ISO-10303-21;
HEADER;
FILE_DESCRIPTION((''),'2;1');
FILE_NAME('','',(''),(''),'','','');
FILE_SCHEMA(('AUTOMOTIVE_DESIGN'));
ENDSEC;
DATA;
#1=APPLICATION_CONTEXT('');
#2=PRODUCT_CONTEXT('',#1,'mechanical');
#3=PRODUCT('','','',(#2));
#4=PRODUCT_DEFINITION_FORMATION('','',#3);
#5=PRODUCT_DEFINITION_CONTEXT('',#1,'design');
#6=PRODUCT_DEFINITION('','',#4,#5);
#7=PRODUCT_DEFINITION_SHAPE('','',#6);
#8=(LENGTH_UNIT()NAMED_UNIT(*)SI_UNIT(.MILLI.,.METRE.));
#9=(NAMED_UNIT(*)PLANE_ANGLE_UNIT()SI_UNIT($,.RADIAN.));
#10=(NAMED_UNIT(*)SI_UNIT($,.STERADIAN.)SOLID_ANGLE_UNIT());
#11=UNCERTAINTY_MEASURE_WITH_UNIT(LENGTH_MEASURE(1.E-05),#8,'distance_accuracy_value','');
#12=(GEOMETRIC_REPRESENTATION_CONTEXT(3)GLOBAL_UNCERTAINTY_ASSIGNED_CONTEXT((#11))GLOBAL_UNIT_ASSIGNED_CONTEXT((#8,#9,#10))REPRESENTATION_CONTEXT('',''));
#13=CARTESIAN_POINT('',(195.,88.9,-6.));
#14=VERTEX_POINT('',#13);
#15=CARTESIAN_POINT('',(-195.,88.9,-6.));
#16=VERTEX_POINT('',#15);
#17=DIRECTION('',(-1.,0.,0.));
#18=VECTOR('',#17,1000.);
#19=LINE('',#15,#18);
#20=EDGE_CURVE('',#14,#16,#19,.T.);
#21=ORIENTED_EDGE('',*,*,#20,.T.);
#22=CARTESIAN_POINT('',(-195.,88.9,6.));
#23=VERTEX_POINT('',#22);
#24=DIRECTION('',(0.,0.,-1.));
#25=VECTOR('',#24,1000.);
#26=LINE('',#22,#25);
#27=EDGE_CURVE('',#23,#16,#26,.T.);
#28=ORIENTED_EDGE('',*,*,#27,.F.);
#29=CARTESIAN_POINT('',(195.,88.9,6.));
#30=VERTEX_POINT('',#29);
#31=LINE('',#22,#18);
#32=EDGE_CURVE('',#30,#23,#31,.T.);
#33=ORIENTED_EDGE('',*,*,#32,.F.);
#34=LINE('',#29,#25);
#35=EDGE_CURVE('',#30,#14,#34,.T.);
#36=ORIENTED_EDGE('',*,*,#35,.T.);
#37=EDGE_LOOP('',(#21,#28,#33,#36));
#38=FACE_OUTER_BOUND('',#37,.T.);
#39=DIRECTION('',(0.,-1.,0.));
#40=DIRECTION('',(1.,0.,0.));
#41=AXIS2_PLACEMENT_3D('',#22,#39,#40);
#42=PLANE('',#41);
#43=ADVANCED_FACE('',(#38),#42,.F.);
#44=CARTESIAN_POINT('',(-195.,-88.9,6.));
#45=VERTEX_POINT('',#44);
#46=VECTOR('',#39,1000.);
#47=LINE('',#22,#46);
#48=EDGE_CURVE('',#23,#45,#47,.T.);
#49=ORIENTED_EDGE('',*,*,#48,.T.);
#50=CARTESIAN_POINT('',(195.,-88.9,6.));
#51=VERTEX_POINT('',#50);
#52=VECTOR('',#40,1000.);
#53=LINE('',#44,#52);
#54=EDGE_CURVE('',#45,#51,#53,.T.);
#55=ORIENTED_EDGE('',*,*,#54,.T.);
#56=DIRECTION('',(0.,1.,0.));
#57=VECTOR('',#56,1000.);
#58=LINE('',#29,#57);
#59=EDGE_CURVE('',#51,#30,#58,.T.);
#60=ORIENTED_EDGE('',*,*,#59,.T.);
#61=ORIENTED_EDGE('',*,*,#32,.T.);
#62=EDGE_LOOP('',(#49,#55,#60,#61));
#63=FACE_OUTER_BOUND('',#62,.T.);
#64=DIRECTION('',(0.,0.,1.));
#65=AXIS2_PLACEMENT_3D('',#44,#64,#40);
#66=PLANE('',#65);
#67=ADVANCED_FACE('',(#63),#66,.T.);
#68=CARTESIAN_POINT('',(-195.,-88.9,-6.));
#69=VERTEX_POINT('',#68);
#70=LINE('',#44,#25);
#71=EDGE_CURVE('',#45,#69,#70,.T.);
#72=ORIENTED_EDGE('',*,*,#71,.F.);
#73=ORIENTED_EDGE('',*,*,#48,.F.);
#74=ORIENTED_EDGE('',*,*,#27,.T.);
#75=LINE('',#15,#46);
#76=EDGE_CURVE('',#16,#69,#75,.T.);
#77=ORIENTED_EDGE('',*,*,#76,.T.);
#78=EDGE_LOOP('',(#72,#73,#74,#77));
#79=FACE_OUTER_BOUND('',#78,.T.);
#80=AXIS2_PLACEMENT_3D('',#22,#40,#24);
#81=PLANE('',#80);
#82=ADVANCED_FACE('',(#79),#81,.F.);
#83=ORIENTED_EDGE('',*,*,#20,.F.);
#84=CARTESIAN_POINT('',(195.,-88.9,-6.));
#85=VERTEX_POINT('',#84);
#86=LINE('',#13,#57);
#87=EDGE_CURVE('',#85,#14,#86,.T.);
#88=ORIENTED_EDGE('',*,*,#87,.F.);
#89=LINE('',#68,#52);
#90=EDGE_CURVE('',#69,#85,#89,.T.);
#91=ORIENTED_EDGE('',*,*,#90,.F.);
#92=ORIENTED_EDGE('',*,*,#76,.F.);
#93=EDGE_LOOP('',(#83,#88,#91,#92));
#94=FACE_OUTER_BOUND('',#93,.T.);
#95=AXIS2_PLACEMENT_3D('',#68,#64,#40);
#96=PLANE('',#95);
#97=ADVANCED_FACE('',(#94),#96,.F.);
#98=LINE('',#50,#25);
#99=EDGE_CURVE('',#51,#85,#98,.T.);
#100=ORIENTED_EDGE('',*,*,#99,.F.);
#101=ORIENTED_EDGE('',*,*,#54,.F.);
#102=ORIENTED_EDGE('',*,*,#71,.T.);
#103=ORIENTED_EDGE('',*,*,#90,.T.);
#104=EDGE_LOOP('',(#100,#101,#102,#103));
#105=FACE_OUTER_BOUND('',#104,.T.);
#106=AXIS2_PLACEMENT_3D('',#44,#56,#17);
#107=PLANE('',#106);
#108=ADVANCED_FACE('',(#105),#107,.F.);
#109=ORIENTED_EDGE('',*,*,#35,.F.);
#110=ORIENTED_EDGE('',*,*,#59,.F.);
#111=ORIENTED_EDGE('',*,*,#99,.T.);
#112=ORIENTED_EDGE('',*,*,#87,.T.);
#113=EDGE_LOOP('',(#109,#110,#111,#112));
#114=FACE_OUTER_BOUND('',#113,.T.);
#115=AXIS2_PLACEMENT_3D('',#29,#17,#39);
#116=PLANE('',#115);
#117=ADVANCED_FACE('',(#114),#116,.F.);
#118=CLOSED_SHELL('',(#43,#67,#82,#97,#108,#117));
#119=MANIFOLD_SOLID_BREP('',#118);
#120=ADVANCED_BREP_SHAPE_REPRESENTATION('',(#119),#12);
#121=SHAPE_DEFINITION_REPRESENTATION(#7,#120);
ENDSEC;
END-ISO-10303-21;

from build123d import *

# Parameters (mm, degrees)
SKETCH1_W      = 390
SKETCH1_H      = 177.8
EXTRUDE1_DEPTH = 6


with BuildPart() as part:
    # Sketch1 → Extrude1 (new, symmetric)
    with BuildSketch(Plane.XY):
        Rectangle(SKETCH1_W, SKETCH1_H)
    extrude(amount=EXTRUDE1_DEPTH, both=True)


solid = part.part
